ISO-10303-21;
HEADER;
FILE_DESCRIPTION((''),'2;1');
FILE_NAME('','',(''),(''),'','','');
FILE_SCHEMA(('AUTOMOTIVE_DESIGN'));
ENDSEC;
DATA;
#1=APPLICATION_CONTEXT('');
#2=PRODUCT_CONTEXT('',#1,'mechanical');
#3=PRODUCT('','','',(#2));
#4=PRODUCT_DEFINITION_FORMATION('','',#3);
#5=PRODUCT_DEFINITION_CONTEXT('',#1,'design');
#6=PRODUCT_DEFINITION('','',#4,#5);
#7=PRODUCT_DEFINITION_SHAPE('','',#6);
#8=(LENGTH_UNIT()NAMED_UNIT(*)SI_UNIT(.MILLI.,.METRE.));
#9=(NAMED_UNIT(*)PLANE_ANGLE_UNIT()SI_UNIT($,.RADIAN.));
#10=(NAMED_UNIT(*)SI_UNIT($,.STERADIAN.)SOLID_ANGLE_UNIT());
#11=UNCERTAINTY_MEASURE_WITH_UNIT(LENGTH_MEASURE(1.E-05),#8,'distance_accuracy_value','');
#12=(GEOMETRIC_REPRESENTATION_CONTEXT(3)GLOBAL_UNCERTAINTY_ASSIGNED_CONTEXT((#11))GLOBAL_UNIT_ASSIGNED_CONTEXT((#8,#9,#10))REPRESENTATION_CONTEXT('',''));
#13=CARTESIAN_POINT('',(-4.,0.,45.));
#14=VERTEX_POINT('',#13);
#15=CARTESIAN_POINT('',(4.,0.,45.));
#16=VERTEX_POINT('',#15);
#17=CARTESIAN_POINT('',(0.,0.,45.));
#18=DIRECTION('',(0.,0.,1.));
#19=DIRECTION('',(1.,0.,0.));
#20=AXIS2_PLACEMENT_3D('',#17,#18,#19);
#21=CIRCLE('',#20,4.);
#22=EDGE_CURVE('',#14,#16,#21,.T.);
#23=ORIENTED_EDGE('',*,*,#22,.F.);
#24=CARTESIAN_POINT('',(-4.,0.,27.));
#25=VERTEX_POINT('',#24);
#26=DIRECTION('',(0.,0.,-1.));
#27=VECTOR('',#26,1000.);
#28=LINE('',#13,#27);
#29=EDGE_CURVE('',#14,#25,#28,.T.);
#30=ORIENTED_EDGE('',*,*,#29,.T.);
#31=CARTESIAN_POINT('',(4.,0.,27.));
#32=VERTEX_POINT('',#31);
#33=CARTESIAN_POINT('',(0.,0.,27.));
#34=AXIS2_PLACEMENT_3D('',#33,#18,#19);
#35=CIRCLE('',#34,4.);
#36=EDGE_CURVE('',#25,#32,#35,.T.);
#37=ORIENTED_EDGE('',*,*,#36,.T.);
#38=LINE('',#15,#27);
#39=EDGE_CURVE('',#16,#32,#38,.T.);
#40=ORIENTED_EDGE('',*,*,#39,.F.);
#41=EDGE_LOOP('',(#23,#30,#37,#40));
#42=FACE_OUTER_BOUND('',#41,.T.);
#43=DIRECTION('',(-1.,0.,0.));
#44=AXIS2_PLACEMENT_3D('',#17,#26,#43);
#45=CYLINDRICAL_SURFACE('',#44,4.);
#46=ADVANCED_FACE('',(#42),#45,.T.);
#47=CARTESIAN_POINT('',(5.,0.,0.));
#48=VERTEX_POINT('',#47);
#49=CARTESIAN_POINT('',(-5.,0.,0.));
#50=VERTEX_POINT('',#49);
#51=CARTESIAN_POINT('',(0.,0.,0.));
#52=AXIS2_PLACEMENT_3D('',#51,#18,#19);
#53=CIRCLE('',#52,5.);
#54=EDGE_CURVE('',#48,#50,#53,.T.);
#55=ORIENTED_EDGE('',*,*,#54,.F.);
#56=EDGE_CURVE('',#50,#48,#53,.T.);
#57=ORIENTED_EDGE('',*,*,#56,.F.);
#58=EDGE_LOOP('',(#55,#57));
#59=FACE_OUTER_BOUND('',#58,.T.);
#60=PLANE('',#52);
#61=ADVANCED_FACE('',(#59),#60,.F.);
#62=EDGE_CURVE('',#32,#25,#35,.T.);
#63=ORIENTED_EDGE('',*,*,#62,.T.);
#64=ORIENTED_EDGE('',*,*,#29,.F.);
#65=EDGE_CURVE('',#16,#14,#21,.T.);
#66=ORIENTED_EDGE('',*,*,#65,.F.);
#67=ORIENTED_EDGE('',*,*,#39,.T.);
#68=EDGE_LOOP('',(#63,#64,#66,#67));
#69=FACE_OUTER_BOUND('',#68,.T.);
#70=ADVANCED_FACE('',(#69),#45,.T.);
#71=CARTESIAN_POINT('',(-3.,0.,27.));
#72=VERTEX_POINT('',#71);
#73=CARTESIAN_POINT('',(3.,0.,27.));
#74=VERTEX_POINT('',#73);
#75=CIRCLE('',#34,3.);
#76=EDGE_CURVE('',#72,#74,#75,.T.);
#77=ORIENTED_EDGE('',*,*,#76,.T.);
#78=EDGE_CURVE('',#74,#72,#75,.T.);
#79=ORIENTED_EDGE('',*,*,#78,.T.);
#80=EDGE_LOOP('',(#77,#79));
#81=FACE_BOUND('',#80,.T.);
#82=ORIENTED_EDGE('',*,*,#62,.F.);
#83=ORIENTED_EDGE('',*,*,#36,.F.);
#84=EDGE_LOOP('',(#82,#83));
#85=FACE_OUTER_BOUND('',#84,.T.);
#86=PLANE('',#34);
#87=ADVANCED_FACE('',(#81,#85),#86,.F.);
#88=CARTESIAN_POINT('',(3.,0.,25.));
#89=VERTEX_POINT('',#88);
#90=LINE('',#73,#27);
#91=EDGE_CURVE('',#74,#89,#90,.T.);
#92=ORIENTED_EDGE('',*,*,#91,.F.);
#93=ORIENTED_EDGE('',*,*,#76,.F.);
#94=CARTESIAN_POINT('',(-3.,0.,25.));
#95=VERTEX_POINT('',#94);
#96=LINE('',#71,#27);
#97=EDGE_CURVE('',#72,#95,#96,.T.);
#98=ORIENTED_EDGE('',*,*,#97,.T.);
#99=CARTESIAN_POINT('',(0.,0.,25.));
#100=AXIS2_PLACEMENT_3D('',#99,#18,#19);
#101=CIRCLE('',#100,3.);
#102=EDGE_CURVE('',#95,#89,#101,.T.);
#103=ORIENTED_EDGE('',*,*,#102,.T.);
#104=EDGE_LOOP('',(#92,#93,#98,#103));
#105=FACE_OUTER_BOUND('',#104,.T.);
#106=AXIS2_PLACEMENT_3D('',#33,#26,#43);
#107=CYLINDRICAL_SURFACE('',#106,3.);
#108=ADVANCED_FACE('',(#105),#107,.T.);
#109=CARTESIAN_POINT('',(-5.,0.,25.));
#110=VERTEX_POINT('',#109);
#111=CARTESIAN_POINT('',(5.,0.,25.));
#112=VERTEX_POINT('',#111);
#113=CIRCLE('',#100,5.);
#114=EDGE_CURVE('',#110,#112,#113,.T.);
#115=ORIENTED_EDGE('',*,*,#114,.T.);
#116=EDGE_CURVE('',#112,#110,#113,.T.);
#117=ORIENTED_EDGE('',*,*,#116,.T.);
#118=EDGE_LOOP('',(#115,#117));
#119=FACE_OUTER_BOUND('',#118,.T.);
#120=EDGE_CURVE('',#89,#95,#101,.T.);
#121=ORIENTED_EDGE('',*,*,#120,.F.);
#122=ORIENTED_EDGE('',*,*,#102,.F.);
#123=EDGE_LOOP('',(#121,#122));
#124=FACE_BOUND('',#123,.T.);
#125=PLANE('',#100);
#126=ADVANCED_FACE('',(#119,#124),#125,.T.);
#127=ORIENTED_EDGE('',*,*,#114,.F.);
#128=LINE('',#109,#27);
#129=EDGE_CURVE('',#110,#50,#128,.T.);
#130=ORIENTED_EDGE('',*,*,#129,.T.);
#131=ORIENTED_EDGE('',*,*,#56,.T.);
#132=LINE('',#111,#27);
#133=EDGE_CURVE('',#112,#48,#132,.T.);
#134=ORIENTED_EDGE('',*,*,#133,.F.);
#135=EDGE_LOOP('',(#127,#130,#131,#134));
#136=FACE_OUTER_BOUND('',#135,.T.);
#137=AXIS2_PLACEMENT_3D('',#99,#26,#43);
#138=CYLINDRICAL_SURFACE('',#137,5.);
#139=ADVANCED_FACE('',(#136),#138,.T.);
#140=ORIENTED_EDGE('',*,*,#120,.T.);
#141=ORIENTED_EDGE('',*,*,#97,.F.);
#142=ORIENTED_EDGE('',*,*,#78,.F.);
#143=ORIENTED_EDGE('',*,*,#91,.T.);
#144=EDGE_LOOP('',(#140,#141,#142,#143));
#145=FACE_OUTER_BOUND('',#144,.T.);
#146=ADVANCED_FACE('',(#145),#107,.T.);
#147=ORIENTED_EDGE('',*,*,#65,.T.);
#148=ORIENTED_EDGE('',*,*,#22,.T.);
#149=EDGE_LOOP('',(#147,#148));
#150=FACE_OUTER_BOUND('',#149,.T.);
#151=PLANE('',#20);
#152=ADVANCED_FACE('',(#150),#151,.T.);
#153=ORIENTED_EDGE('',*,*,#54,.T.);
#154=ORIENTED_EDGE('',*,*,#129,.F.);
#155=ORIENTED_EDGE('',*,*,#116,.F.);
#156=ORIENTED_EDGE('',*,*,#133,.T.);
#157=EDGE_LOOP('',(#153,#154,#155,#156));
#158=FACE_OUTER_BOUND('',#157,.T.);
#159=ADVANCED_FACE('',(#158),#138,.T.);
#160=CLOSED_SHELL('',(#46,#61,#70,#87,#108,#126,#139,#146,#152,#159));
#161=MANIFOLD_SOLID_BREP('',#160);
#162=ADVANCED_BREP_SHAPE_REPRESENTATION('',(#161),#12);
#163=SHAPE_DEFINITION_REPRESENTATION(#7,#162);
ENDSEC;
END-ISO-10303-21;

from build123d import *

# Parameters (mm, degrees)
SKETCH1_R           = 5
BOSS_EXTRUDE1_DEPTH = 25
SKETCH2_R           = 4
BOSS_EXTRUDE2_DEPTH = 20
SKETCH3_OUTSIDE_W   = 21.434
SKETCH3_OUTSIDE_H   = 21.434
SKETCH3_OUTSIDE_R   = 3
CUT_EXTRUDE1_DEPTH  = 2


with BuildPart() as part:
    # Sketch1 → Boss-Extrude1 (new body)
    with BuildSketch(Plane.XY):
        Circle(SKETCH1_R)
    extrude(amount=BOSS_EXTRUDE1_DEPTH)

    # Sketch2 → Boss-Extrude2 (add)
    with BuildSketch(Plane.XY.offset(25)):
        Circle(SKETCH2_R)
    extrude(amount=BOSS_EXTRUDE2_DEPTH)

    # Sketch3 outside → Cut-Extrude1 (cut)
    with BuildSketch(Plane.XY.offset(25)):
        Rectangle(SKETCH3_OUTSIDE_W, SKETCH3_OUTSIDE_H)
        Circle(SKETCH3_OUTSIDE_R, mode=Mode.SUBTRACT)
    extrude(amount=CUT_EXTRUDE1_DEPTH, mode=Mode.SUBTRACT)


solid = part.part
